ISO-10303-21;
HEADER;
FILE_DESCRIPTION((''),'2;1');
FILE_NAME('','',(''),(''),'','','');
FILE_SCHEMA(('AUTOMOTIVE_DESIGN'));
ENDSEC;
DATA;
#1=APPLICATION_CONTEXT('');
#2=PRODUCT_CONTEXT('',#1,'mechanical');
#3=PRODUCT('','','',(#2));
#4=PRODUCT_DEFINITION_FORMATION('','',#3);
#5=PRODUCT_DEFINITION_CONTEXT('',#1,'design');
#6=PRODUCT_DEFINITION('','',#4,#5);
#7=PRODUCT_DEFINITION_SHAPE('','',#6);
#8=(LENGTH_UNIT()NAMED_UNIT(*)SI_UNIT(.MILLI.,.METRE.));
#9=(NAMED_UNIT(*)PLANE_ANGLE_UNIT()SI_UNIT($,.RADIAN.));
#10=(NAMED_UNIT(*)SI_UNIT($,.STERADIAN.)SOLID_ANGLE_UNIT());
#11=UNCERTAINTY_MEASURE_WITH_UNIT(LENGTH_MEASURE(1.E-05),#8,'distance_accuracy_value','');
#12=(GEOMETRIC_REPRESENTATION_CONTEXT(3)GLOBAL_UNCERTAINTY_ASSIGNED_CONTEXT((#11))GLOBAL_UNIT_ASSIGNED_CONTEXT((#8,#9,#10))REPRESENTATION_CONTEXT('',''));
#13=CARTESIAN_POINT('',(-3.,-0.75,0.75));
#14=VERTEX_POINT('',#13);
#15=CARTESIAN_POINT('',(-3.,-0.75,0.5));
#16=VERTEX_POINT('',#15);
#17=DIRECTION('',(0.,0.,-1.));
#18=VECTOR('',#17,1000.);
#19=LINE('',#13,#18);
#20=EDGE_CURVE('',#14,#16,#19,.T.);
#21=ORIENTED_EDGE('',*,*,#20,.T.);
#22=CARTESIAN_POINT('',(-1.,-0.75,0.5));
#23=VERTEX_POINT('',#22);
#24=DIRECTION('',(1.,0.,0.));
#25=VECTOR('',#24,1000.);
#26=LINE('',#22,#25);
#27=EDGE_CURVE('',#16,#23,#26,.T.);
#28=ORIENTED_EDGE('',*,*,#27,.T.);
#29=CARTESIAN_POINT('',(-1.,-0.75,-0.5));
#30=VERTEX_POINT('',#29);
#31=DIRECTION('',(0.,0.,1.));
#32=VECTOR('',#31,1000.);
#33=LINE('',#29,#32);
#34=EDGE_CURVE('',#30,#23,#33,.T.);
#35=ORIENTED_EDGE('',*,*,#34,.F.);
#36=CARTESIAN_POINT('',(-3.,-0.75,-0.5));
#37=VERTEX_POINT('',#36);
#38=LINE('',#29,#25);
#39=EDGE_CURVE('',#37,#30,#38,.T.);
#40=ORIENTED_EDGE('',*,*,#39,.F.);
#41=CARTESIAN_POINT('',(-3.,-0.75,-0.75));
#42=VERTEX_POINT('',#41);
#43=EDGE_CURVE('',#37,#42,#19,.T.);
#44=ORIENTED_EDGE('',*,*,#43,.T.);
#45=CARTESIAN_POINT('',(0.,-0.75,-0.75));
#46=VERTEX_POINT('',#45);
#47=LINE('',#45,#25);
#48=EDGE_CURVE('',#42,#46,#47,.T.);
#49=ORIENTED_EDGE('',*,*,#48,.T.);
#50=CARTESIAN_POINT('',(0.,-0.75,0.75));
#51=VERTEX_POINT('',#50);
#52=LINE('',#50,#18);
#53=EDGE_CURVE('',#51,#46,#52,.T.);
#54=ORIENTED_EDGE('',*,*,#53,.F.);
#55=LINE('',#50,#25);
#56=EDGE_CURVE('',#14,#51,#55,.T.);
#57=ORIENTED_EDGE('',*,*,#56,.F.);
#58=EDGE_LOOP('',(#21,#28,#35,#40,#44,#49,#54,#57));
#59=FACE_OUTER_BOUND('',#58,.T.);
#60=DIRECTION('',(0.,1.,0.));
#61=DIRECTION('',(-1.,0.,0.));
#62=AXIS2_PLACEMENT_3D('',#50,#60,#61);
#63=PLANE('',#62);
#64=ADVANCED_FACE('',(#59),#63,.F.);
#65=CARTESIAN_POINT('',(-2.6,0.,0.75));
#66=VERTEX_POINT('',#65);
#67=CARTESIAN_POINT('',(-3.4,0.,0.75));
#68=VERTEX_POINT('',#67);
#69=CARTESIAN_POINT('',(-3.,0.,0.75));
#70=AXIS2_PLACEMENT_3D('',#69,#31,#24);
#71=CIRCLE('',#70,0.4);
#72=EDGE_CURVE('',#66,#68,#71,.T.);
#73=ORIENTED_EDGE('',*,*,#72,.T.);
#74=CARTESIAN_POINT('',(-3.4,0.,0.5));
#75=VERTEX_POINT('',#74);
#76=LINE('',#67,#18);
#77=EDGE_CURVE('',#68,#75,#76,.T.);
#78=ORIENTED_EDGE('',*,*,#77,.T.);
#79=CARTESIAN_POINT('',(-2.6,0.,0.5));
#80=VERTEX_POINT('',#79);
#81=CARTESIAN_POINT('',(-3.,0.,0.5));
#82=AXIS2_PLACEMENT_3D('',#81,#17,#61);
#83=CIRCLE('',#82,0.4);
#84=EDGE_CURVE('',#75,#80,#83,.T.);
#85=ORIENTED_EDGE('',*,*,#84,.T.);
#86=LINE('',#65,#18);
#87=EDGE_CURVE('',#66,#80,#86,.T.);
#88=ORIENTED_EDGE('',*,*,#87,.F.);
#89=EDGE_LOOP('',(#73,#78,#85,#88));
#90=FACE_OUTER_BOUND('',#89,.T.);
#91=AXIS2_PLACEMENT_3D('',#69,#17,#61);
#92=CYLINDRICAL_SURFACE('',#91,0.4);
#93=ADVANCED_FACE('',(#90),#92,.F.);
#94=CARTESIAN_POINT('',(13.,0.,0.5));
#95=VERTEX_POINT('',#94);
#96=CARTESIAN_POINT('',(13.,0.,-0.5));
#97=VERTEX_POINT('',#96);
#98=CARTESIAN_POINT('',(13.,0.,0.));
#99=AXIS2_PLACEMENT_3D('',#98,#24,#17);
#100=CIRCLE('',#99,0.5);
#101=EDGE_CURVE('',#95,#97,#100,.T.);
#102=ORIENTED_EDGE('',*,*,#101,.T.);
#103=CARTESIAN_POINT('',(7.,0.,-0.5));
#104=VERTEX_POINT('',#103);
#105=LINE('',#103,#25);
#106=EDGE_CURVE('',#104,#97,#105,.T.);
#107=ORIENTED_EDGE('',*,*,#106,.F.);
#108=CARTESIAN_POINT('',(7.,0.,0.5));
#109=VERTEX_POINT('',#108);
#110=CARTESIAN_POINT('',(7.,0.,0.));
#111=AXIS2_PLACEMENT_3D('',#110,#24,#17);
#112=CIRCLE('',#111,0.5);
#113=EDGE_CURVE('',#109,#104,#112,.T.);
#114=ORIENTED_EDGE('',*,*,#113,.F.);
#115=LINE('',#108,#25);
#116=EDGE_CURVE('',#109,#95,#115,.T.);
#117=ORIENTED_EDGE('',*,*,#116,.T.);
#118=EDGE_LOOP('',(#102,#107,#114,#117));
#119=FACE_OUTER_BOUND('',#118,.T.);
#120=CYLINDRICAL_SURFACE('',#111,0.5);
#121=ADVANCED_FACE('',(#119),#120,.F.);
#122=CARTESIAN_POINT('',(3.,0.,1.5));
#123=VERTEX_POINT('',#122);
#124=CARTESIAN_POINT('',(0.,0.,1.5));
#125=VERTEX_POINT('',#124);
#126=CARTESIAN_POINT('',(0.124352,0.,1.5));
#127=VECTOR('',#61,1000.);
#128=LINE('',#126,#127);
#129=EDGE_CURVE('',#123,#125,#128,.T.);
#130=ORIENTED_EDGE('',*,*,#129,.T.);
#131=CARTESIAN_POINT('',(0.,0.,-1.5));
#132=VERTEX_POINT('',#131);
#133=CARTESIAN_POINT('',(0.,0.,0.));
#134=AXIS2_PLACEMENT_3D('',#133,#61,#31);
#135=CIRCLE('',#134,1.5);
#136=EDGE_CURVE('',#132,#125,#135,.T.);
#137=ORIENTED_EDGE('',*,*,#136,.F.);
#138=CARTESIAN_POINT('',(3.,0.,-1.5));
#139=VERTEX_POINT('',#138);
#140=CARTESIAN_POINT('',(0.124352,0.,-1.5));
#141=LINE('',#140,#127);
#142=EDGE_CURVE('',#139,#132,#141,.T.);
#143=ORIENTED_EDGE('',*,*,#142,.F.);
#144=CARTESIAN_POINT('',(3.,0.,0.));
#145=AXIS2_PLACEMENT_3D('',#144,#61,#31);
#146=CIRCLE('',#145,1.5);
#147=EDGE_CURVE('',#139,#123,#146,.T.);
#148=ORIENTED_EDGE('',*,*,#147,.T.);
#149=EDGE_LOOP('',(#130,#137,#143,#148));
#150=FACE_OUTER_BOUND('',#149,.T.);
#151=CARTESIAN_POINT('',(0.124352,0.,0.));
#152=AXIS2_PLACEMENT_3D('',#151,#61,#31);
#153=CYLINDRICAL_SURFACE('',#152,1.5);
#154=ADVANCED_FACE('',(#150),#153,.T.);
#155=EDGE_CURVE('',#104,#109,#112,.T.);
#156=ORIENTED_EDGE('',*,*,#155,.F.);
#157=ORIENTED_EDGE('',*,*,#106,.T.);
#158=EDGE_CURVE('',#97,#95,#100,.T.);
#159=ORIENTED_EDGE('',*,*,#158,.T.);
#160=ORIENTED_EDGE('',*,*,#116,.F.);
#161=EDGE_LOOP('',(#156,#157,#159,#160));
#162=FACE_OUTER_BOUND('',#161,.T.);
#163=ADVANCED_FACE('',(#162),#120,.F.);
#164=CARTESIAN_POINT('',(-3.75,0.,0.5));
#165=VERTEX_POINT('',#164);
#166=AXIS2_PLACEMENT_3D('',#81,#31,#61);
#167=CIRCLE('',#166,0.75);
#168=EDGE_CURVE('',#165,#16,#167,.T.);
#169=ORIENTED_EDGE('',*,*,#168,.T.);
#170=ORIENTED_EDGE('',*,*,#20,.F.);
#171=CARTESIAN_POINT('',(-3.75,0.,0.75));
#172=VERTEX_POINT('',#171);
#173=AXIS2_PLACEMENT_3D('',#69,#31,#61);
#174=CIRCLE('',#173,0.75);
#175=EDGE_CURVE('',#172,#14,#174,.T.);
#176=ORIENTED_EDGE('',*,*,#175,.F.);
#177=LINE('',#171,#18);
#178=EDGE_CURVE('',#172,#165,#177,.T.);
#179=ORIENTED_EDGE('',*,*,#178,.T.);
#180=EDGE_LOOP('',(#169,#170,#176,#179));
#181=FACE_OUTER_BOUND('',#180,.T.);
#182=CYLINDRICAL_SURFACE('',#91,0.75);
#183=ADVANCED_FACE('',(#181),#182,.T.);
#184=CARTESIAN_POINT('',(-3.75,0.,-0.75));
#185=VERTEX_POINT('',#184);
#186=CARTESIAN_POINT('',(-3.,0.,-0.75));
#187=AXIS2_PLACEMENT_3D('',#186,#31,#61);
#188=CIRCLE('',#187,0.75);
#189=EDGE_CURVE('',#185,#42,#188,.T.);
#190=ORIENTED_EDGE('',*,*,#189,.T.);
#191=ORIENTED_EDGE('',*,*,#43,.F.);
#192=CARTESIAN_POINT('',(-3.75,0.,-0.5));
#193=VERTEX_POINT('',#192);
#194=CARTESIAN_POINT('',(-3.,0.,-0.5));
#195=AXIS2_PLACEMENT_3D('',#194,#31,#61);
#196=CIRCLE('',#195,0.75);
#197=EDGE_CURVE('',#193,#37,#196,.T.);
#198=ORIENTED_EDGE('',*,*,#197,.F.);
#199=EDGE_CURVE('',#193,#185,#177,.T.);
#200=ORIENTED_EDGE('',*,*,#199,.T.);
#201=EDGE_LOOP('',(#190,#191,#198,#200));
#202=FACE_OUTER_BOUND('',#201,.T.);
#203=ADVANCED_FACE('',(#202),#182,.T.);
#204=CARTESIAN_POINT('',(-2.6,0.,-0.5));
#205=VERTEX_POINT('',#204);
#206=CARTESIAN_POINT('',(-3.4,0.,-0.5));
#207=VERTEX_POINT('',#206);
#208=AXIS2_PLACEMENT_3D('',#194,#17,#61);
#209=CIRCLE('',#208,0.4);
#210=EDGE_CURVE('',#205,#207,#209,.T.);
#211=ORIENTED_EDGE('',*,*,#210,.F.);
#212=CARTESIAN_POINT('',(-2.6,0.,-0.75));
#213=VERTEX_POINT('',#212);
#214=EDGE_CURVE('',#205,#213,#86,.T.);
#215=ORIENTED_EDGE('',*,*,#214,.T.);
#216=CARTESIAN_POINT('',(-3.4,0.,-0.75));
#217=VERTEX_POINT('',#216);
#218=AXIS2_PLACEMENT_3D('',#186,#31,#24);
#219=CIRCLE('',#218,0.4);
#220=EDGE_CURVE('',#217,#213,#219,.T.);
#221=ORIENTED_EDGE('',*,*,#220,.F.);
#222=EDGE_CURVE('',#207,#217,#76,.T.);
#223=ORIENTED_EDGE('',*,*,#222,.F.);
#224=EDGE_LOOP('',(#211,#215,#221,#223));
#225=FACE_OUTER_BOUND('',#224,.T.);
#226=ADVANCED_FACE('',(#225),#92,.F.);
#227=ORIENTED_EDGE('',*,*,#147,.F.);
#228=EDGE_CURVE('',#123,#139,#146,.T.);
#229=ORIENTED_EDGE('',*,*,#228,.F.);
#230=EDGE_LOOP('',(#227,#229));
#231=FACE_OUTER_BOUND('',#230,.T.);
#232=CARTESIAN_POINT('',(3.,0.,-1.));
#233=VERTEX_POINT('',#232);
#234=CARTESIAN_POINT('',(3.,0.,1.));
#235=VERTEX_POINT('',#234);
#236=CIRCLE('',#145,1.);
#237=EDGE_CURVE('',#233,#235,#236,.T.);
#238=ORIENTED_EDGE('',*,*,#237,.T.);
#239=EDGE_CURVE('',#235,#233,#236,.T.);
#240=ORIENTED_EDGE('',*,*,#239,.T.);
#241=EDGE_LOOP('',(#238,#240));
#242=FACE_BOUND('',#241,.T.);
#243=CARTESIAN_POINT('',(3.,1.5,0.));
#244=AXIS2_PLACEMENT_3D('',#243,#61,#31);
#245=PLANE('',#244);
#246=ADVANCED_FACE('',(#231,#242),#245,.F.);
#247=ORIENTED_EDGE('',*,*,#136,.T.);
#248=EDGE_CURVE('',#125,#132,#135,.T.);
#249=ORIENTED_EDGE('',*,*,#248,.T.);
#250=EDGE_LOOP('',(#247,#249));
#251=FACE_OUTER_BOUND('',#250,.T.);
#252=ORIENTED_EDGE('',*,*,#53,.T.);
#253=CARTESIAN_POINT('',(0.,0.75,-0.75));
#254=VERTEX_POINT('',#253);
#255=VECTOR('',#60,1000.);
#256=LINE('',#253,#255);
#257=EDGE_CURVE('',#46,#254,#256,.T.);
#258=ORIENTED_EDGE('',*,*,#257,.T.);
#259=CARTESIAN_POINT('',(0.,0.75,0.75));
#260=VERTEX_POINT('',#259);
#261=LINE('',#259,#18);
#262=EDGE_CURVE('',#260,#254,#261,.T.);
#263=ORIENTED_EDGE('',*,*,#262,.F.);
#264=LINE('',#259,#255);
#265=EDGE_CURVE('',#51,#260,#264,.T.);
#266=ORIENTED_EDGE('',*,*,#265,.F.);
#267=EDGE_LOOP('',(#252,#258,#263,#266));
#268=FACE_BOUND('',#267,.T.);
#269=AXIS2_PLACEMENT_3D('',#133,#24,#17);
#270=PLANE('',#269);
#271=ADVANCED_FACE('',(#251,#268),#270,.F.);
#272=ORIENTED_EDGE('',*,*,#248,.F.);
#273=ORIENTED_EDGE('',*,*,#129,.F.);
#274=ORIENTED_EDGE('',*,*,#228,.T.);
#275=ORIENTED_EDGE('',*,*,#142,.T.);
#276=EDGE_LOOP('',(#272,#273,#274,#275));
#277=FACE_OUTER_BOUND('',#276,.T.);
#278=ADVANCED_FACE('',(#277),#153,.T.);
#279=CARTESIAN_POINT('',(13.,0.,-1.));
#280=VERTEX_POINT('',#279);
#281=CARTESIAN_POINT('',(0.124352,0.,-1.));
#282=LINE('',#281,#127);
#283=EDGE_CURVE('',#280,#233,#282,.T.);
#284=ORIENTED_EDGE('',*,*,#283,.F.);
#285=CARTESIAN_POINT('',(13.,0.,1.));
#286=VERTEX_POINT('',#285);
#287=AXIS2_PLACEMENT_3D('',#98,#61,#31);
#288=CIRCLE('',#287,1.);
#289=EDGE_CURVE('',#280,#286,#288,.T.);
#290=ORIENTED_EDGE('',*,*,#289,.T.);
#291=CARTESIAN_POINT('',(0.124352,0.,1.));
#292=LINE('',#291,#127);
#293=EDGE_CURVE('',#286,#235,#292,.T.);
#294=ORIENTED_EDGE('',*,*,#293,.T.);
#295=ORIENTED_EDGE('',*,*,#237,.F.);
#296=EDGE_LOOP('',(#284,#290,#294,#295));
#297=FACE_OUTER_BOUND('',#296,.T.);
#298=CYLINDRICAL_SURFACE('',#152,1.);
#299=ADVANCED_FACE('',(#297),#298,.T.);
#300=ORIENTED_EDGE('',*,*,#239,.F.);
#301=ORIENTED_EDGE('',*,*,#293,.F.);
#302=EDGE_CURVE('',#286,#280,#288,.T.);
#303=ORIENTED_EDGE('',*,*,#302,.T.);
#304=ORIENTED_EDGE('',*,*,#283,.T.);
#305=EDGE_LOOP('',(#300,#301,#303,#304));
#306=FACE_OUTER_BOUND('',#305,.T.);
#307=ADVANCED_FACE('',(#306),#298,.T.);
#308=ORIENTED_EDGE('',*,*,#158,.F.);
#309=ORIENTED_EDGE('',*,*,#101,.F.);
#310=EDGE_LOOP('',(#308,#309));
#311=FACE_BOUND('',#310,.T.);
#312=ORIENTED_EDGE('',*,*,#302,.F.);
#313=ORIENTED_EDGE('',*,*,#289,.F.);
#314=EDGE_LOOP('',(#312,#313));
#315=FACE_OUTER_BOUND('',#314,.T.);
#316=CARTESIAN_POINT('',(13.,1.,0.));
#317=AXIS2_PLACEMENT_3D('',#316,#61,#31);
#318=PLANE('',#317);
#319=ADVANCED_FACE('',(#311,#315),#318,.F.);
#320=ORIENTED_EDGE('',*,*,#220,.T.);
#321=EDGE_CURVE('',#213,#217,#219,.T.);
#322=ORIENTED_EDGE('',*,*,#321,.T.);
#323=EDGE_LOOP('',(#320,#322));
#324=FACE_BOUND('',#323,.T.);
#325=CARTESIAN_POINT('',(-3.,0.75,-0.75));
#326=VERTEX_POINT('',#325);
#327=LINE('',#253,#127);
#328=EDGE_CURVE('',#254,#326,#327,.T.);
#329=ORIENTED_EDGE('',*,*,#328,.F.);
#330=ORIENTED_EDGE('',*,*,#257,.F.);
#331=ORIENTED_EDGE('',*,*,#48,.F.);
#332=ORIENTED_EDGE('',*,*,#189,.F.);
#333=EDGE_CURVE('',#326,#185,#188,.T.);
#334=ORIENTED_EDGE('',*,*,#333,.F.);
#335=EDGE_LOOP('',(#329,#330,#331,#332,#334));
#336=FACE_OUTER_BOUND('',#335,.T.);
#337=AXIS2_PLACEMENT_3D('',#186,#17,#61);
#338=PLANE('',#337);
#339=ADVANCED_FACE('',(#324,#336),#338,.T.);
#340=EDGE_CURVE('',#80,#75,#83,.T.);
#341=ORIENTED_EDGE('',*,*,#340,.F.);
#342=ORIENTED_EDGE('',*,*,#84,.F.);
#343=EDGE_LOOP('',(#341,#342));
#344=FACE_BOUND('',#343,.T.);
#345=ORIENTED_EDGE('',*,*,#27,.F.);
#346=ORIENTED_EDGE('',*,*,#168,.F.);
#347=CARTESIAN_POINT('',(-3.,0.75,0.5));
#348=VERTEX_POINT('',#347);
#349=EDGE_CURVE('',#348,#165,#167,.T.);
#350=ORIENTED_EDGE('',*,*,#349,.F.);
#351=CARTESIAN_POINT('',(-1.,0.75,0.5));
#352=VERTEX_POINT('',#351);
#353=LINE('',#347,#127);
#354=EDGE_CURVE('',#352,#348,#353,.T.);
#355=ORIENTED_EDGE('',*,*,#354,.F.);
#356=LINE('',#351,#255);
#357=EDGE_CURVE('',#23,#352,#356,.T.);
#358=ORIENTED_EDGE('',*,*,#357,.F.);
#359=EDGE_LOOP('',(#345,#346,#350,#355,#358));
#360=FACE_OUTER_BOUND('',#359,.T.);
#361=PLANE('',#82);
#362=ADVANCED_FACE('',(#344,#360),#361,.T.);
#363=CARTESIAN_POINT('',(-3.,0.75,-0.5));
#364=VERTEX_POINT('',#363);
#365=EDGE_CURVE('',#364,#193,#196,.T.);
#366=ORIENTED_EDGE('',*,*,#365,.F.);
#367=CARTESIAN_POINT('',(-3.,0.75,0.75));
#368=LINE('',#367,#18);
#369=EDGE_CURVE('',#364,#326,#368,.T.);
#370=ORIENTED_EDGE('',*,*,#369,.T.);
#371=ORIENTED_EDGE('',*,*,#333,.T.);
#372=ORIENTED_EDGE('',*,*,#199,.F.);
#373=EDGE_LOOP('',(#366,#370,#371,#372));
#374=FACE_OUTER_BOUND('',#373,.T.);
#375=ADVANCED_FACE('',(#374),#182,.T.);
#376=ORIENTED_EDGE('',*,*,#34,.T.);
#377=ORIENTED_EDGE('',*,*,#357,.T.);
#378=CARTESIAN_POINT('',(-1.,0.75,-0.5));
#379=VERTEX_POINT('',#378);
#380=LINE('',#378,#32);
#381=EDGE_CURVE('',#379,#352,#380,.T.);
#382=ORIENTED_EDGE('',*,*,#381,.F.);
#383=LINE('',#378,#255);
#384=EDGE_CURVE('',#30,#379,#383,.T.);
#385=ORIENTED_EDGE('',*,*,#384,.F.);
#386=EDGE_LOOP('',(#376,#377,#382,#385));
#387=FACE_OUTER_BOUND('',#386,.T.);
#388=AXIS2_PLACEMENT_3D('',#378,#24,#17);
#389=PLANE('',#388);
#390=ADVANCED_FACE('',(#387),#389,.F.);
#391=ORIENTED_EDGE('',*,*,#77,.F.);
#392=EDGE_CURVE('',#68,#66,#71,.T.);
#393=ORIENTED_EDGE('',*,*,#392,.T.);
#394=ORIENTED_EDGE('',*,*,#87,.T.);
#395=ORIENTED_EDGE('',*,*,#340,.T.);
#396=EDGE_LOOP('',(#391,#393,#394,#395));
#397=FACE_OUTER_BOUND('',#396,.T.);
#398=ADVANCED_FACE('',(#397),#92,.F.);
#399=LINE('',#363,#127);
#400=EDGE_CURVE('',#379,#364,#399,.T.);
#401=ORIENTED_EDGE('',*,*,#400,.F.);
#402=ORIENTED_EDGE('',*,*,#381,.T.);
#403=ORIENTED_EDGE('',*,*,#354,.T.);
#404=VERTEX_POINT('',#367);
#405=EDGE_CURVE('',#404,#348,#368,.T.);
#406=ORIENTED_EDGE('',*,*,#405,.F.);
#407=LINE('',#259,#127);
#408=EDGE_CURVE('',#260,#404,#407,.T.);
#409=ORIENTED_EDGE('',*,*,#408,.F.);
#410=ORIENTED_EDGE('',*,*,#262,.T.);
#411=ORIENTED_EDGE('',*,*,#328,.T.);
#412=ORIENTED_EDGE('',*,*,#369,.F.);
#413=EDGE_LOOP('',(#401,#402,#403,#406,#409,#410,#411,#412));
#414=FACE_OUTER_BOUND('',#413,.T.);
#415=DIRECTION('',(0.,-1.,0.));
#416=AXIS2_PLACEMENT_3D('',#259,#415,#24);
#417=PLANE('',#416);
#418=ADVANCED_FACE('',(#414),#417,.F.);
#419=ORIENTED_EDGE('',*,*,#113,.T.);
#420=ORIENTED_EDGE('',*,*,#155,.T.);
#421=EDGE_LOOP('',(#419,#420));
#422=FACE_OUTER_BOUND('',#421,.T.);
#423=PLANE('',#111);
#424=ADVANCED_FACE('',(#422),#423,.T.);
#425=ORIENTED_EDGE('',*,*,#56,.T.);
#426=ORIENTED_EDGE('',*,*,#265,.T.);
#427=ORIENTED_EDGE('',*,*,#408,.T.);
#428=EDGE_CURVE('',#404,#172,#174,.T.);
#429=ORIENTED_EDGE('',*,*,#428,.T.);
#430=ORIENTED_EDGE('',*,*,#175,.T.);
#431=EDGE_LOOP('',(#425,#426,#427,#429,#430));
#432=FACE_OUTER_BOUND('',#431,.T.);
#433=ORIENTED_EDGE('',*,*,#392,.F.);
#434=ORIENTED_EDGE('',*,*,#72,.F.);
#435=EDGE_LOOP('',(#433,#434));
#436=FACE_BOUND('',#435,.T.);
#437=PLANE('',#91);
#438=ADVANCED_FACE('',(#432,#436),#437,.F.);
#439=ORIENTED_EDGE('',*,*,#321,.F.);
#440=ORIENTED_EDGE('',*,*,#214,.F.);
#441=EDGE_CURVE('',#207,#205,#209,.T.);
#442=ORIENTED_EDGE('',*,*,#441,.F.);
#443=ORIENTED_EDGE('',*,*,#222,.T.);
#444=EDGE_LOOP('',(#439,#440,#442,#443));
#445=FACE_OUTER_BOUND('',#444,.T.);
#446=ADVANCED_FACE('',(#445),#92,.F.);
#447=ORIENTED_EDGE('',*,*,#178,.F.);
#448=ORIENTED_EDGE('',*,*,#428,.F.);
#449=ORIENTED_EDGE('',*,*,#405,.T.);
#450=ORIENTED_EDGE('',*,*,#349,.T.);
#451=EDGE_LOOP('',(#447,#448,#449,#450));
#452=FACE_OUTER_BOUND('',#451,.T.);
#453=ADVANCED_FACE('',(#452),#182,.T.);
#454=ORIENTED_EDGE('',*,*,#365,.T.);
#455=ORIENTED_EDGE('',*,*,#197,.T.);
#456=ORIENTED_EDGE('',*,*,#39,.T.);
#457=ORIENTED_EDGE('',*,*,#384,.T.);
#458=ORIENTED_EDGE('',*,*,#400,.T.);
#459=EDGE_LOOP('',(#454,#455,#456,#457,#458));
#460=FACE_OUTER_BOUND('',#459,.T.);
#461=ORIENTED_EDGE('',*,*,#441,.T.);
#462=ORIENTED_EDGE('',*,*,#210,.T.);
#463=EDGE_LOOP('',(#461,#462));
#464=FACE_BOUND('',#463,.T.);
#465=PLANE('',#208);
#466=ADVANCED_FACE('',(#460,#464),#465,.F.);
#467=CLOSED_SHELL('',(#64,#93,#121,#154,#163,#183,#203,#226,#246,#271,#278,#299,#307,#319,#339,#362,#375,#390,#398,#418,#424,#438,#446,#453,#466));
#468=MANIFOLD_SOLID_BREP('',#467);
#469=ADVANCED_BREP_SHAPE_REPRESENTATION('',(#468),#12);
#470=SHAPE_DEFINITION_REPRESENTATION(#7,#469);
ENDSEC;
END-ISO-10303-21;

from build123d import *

# Parameters (mm, degrees)
SKETCH2_R           = 0.4
BOSS_EXTRUDE1_DEPTH = 0.75
CUT_EXTRUDE1_DEPTH  = 0.5
SKETCH4_R           = 0.5
CUT_EXTRUDE2_DEPTH  = 6


with BuildPart() as part:
    # Sketch1 → Revolve1 (revolve)
    with BuildSketch(Plane.XY, mode=Mode.PRIVATE) as revolve1_sk:
        Polygon((0, 0), (0, 1.5), (3, 1.5), (3, 1), (13, 1), (13, 0), align=None)
    revolve(revolve1_sk.sketch.rotate(Axis((0.124352332, 0, 0), (1, 0, 0)), 90), axis=Axis((0.124352332, 0, 0), (1, 0, 0)))

    # Sketch2 → Boss-Extrude1 (add, symmetric)
    with BuildSketch(Plane.XY):
        with BuildLine():
            Line((0, 0.75), (0, -0.75))
            Line((0, -0.75), (-3, -0.75))
            ThreePointArc((-3, -0.75), (-3.75, 0), (-3, 0.75))
            Line((-3, 0.75), (0, 0.75))
        make_face()
        with Locations((-3, 0)):
            Circle(SKETCH2_R, mode=Mode.SUBTRACT)
    extrude(amount=BOSS_EXTRUDE1_DEPTH, both=True)

    # Sketch3 → Cut-Extrude1 (cut, symmetric)
    with BuildSketch(Plane.XY):
        with BuildLine():
            Line((-1, 0.75), (-1, -0.75))
            Line((-1, -0.75), (-3, -0.75))
            ThreePointArc((-3, -0.75), (-3.75, 0), (-3, 0.75))
            Line((-3, 0.75), (-1, 0.75))
        make_face()
    extrude(amount=CUT_EXTRUDE1_DEPTH, both=True, mode=Mode.SUBTRACT)

    # Sketch4 → Cut-Extrude2 (cut)
    with BuildSketch(Plane(origin=(13, 0, 0), x_dir=(0, 0, -1), z_dir=(1, 0, 0))):
        Circle(SKETCH4_R)
    extrude(amount=-CUT_EXTRUDE2_DEPTH, mode=Mode.SUBTRACT)


solid = part.part
